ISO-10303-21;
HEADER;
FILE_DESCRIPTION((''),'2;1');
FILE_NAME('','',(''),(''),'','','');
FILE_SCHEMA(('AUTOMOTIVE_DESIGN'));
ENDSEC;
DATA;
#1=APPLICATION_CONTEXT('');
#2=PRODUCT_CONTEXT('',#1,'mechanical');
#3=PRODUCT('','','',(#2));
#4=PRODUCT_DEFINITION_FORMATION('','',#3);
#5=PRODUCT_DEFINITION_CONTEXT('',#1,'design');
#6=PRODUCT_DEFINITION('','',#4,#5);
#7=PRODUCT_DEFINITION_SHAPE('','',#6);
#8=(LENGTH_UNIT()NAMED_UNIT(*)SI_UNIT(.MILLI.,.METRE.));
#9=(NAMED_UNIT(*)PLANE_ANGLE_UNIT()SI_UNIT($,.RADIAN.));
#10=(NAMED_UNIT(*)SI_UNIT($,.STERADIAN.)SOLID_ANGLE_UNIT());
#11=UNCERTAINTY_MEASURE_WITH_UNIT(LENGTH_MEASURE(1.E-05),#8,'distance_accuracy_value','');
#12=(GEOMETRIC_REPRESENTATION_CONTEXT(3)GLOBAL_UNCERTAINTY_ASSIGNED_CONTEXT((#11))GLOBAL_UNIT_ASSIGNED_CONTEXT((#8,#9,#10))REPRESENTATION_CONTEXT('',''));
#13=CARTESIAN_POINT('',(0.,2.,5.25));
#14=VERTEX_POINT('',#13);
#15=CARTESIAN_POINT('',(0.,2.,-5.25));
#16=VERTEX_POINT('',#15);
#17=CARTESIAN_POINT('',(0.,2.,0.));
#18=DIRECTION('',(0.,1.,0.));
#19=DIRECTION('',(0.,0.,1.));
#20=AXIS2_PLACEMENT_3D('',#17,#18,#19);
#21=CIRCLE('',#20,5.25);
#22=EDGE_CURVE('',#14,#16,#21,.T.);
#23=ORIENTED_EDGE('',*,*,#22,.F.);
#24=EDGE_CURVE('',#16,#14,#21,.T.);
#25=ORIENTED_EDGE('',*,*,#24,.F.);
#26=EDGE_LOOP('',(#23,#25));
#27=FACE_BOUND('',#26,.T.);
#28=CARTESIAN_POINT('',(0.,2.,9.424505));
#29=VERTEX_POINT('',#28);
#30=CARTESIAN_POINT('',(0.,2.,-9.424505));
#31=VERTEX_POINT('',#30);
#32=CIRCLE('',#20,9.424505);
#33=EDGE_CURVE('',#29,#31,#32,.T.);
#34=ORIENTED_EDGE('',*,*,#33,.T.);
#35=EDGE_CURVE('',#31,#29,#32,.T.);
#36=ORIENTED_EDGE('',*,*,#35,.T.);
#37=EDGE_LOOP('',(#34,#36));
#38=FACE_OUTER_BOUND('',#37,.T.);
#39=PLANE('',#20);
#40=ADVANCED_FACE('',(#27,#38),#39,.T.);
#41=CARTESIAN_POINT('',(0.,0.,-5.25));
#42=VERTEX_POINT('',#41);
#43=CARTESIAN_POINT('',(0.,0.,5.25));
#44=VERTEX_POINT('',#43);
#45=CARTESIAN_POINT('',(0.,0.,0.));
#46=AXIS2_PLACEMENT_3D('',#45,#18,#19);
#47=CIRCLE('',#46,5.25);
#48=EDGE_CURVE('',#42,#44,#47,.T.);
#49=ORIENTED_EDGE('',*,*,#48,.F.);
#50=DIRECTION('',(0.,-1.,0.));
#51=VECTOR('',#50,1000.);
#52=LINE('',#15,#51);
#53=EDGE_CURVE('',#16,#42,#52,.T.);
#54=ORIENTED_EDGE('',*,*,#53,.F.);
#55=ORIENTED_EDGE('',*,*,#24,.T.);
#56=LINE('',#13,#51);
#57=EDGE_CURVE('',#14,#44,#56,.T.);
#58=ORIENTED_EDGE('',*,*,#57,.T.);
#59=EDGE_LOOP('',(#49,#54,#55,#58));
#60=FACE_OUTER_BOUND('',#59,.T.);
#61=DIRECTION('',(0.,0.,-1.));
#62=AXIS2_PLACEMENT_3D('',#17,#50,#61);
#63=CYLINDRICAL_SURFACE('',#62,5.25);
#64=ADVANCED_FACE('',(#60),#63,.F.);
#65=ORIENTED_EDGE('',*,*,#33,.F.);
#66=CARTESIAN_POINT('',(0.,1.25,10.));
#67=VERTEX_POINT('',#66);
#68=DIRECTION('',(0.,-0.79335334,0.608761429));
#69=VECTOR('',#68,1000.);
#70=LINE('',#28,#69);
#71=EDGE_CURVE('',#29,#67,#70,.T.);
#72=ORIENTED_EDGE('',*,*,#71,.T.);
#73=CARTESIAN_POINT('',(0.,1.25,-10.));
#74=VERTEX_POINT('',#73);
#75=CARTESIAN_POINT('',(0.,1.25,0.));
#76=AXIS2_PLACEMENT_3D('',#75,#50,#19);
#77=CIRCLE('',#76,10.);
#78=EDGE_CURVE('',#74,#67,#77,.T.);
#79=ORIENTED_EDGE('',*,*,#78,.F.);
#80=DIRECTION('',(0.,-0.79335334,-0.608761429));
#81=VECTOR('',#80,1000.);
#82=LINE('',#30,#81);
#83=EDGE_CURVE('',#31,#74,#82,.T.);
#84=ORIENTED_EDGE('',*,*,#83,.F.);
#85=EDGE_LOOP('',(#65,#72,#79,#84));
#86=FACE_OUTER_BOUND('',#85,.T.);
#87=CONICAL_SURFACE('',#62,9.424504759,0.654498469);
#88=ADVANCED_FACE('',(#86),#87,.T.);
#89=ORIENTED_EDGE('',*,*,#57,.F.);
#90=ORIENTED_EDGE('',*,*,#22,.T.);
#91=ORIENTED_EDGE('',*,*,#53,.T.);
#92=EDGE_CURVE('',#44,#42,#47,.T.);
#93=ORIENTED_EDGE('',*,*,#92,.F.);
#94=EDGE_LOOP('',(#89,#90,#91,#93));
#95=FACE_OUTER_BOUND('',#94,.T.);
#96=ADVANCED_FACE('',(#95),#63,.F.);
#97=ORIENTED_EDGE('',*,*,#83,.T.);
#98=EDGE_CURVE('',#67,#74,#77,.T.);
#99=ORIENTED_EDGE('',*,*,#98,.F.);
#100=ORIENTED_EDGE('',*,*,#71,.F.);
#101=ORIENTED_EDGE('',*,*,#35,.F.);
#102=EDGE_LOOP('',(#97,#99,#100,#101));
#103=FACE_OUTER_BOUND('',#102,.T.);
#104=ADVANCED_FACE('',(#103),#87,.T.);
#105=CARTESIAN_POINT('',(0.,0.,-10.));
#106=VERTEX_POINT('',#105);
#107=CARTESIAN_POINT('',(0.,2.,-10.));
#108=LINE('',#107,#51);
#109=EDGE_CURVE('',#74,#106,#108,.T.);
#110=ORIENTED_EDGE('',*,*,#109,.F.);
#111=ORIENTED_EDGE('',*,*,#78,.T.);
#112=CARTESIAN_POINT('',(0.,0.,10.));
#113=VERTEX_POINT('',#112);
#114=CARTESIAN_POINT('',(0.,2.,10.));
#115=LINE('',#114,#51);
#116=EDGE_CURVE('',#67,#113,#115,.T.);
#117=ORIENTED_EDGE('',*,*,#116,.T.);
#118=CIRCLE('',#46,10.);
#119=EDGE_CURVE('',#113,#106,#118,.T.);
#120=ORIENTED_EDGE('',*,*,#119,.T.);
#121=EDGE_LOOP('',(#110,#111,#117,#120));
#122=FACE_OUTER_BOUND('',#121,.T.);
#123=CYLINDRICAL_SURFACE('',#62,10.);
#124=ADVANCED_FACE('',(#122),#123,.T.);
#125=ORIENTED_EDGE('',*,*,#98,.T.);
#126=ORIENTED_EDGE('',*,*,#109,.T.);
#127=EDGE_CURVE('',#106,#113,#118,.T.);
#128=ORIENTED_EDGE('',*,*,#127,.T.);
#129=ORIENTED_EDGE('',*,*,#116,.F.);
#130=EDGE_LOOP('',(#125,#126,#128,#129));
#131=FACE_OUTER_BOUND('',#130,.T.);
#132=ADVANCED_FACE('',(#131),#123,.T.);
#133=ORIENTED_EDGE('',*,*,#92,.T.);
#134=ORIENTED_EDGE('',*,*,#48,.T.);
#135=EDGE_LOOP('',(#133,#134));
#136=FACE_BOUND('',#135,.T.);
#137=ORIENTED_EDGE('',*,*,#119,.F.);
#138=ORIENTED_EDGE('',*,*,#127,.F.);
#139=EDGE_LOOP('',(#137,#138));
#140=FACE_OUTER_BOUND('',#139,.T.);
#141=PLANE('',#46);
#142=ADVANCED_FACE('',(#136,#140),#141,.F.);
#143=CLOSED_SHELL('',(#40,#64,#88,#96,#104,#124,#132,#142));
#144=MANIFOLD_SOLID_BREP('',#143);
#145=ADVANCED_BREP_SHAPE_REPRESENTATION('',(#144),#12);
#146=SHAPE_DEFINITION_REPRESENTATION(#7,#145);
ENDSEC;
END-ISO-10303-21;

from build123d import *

# Parameters (mm, degrees)
SKETCH1_R           = 10
SKETCH1_R_2         = 5.25
BOSS_EXTRUDE1_DEPTH = 2
CHAMFER1_SIZE       = 0.75
CHAMFER1_SIZE2      = 0.575495241


with BuildPart() as part:
    # Sketch1 → Boss-Extrude1 (new body)
    with BuildSketch(Plane(origin=(0, 0, 0), x_dir=(1, 0, 0), z_dir=(0, 1, 0))):
        with Locations(Location((0, 0, 0), (0, 0, 270))):
            Circle(SKETCH1_R)
        with Locations(Location((0, 0, 0), (0, 0, 270))):
            Circle(SKETCH1_R_2, mode=Mode.SUBTRACT)
    extrude(amount=BOSS_EXTRUDE1_DEPTH)

    # Chamfer1
    chamfer1_edges = [part.edges().sort_by_distance(p)[0] for p in [
        (0, 2, -10),
    ]]
    chamfer1_side = [part.faces().sort_by_distance(p)[0] for p in [
        (0, 1, -10),
    ]]
    chamfer(chamfer1_edges, length=CHAMFER1_SIZE, length2=CHAMFER1_SIZE2, reference=chamfer1_side[0])


solid = part.part
